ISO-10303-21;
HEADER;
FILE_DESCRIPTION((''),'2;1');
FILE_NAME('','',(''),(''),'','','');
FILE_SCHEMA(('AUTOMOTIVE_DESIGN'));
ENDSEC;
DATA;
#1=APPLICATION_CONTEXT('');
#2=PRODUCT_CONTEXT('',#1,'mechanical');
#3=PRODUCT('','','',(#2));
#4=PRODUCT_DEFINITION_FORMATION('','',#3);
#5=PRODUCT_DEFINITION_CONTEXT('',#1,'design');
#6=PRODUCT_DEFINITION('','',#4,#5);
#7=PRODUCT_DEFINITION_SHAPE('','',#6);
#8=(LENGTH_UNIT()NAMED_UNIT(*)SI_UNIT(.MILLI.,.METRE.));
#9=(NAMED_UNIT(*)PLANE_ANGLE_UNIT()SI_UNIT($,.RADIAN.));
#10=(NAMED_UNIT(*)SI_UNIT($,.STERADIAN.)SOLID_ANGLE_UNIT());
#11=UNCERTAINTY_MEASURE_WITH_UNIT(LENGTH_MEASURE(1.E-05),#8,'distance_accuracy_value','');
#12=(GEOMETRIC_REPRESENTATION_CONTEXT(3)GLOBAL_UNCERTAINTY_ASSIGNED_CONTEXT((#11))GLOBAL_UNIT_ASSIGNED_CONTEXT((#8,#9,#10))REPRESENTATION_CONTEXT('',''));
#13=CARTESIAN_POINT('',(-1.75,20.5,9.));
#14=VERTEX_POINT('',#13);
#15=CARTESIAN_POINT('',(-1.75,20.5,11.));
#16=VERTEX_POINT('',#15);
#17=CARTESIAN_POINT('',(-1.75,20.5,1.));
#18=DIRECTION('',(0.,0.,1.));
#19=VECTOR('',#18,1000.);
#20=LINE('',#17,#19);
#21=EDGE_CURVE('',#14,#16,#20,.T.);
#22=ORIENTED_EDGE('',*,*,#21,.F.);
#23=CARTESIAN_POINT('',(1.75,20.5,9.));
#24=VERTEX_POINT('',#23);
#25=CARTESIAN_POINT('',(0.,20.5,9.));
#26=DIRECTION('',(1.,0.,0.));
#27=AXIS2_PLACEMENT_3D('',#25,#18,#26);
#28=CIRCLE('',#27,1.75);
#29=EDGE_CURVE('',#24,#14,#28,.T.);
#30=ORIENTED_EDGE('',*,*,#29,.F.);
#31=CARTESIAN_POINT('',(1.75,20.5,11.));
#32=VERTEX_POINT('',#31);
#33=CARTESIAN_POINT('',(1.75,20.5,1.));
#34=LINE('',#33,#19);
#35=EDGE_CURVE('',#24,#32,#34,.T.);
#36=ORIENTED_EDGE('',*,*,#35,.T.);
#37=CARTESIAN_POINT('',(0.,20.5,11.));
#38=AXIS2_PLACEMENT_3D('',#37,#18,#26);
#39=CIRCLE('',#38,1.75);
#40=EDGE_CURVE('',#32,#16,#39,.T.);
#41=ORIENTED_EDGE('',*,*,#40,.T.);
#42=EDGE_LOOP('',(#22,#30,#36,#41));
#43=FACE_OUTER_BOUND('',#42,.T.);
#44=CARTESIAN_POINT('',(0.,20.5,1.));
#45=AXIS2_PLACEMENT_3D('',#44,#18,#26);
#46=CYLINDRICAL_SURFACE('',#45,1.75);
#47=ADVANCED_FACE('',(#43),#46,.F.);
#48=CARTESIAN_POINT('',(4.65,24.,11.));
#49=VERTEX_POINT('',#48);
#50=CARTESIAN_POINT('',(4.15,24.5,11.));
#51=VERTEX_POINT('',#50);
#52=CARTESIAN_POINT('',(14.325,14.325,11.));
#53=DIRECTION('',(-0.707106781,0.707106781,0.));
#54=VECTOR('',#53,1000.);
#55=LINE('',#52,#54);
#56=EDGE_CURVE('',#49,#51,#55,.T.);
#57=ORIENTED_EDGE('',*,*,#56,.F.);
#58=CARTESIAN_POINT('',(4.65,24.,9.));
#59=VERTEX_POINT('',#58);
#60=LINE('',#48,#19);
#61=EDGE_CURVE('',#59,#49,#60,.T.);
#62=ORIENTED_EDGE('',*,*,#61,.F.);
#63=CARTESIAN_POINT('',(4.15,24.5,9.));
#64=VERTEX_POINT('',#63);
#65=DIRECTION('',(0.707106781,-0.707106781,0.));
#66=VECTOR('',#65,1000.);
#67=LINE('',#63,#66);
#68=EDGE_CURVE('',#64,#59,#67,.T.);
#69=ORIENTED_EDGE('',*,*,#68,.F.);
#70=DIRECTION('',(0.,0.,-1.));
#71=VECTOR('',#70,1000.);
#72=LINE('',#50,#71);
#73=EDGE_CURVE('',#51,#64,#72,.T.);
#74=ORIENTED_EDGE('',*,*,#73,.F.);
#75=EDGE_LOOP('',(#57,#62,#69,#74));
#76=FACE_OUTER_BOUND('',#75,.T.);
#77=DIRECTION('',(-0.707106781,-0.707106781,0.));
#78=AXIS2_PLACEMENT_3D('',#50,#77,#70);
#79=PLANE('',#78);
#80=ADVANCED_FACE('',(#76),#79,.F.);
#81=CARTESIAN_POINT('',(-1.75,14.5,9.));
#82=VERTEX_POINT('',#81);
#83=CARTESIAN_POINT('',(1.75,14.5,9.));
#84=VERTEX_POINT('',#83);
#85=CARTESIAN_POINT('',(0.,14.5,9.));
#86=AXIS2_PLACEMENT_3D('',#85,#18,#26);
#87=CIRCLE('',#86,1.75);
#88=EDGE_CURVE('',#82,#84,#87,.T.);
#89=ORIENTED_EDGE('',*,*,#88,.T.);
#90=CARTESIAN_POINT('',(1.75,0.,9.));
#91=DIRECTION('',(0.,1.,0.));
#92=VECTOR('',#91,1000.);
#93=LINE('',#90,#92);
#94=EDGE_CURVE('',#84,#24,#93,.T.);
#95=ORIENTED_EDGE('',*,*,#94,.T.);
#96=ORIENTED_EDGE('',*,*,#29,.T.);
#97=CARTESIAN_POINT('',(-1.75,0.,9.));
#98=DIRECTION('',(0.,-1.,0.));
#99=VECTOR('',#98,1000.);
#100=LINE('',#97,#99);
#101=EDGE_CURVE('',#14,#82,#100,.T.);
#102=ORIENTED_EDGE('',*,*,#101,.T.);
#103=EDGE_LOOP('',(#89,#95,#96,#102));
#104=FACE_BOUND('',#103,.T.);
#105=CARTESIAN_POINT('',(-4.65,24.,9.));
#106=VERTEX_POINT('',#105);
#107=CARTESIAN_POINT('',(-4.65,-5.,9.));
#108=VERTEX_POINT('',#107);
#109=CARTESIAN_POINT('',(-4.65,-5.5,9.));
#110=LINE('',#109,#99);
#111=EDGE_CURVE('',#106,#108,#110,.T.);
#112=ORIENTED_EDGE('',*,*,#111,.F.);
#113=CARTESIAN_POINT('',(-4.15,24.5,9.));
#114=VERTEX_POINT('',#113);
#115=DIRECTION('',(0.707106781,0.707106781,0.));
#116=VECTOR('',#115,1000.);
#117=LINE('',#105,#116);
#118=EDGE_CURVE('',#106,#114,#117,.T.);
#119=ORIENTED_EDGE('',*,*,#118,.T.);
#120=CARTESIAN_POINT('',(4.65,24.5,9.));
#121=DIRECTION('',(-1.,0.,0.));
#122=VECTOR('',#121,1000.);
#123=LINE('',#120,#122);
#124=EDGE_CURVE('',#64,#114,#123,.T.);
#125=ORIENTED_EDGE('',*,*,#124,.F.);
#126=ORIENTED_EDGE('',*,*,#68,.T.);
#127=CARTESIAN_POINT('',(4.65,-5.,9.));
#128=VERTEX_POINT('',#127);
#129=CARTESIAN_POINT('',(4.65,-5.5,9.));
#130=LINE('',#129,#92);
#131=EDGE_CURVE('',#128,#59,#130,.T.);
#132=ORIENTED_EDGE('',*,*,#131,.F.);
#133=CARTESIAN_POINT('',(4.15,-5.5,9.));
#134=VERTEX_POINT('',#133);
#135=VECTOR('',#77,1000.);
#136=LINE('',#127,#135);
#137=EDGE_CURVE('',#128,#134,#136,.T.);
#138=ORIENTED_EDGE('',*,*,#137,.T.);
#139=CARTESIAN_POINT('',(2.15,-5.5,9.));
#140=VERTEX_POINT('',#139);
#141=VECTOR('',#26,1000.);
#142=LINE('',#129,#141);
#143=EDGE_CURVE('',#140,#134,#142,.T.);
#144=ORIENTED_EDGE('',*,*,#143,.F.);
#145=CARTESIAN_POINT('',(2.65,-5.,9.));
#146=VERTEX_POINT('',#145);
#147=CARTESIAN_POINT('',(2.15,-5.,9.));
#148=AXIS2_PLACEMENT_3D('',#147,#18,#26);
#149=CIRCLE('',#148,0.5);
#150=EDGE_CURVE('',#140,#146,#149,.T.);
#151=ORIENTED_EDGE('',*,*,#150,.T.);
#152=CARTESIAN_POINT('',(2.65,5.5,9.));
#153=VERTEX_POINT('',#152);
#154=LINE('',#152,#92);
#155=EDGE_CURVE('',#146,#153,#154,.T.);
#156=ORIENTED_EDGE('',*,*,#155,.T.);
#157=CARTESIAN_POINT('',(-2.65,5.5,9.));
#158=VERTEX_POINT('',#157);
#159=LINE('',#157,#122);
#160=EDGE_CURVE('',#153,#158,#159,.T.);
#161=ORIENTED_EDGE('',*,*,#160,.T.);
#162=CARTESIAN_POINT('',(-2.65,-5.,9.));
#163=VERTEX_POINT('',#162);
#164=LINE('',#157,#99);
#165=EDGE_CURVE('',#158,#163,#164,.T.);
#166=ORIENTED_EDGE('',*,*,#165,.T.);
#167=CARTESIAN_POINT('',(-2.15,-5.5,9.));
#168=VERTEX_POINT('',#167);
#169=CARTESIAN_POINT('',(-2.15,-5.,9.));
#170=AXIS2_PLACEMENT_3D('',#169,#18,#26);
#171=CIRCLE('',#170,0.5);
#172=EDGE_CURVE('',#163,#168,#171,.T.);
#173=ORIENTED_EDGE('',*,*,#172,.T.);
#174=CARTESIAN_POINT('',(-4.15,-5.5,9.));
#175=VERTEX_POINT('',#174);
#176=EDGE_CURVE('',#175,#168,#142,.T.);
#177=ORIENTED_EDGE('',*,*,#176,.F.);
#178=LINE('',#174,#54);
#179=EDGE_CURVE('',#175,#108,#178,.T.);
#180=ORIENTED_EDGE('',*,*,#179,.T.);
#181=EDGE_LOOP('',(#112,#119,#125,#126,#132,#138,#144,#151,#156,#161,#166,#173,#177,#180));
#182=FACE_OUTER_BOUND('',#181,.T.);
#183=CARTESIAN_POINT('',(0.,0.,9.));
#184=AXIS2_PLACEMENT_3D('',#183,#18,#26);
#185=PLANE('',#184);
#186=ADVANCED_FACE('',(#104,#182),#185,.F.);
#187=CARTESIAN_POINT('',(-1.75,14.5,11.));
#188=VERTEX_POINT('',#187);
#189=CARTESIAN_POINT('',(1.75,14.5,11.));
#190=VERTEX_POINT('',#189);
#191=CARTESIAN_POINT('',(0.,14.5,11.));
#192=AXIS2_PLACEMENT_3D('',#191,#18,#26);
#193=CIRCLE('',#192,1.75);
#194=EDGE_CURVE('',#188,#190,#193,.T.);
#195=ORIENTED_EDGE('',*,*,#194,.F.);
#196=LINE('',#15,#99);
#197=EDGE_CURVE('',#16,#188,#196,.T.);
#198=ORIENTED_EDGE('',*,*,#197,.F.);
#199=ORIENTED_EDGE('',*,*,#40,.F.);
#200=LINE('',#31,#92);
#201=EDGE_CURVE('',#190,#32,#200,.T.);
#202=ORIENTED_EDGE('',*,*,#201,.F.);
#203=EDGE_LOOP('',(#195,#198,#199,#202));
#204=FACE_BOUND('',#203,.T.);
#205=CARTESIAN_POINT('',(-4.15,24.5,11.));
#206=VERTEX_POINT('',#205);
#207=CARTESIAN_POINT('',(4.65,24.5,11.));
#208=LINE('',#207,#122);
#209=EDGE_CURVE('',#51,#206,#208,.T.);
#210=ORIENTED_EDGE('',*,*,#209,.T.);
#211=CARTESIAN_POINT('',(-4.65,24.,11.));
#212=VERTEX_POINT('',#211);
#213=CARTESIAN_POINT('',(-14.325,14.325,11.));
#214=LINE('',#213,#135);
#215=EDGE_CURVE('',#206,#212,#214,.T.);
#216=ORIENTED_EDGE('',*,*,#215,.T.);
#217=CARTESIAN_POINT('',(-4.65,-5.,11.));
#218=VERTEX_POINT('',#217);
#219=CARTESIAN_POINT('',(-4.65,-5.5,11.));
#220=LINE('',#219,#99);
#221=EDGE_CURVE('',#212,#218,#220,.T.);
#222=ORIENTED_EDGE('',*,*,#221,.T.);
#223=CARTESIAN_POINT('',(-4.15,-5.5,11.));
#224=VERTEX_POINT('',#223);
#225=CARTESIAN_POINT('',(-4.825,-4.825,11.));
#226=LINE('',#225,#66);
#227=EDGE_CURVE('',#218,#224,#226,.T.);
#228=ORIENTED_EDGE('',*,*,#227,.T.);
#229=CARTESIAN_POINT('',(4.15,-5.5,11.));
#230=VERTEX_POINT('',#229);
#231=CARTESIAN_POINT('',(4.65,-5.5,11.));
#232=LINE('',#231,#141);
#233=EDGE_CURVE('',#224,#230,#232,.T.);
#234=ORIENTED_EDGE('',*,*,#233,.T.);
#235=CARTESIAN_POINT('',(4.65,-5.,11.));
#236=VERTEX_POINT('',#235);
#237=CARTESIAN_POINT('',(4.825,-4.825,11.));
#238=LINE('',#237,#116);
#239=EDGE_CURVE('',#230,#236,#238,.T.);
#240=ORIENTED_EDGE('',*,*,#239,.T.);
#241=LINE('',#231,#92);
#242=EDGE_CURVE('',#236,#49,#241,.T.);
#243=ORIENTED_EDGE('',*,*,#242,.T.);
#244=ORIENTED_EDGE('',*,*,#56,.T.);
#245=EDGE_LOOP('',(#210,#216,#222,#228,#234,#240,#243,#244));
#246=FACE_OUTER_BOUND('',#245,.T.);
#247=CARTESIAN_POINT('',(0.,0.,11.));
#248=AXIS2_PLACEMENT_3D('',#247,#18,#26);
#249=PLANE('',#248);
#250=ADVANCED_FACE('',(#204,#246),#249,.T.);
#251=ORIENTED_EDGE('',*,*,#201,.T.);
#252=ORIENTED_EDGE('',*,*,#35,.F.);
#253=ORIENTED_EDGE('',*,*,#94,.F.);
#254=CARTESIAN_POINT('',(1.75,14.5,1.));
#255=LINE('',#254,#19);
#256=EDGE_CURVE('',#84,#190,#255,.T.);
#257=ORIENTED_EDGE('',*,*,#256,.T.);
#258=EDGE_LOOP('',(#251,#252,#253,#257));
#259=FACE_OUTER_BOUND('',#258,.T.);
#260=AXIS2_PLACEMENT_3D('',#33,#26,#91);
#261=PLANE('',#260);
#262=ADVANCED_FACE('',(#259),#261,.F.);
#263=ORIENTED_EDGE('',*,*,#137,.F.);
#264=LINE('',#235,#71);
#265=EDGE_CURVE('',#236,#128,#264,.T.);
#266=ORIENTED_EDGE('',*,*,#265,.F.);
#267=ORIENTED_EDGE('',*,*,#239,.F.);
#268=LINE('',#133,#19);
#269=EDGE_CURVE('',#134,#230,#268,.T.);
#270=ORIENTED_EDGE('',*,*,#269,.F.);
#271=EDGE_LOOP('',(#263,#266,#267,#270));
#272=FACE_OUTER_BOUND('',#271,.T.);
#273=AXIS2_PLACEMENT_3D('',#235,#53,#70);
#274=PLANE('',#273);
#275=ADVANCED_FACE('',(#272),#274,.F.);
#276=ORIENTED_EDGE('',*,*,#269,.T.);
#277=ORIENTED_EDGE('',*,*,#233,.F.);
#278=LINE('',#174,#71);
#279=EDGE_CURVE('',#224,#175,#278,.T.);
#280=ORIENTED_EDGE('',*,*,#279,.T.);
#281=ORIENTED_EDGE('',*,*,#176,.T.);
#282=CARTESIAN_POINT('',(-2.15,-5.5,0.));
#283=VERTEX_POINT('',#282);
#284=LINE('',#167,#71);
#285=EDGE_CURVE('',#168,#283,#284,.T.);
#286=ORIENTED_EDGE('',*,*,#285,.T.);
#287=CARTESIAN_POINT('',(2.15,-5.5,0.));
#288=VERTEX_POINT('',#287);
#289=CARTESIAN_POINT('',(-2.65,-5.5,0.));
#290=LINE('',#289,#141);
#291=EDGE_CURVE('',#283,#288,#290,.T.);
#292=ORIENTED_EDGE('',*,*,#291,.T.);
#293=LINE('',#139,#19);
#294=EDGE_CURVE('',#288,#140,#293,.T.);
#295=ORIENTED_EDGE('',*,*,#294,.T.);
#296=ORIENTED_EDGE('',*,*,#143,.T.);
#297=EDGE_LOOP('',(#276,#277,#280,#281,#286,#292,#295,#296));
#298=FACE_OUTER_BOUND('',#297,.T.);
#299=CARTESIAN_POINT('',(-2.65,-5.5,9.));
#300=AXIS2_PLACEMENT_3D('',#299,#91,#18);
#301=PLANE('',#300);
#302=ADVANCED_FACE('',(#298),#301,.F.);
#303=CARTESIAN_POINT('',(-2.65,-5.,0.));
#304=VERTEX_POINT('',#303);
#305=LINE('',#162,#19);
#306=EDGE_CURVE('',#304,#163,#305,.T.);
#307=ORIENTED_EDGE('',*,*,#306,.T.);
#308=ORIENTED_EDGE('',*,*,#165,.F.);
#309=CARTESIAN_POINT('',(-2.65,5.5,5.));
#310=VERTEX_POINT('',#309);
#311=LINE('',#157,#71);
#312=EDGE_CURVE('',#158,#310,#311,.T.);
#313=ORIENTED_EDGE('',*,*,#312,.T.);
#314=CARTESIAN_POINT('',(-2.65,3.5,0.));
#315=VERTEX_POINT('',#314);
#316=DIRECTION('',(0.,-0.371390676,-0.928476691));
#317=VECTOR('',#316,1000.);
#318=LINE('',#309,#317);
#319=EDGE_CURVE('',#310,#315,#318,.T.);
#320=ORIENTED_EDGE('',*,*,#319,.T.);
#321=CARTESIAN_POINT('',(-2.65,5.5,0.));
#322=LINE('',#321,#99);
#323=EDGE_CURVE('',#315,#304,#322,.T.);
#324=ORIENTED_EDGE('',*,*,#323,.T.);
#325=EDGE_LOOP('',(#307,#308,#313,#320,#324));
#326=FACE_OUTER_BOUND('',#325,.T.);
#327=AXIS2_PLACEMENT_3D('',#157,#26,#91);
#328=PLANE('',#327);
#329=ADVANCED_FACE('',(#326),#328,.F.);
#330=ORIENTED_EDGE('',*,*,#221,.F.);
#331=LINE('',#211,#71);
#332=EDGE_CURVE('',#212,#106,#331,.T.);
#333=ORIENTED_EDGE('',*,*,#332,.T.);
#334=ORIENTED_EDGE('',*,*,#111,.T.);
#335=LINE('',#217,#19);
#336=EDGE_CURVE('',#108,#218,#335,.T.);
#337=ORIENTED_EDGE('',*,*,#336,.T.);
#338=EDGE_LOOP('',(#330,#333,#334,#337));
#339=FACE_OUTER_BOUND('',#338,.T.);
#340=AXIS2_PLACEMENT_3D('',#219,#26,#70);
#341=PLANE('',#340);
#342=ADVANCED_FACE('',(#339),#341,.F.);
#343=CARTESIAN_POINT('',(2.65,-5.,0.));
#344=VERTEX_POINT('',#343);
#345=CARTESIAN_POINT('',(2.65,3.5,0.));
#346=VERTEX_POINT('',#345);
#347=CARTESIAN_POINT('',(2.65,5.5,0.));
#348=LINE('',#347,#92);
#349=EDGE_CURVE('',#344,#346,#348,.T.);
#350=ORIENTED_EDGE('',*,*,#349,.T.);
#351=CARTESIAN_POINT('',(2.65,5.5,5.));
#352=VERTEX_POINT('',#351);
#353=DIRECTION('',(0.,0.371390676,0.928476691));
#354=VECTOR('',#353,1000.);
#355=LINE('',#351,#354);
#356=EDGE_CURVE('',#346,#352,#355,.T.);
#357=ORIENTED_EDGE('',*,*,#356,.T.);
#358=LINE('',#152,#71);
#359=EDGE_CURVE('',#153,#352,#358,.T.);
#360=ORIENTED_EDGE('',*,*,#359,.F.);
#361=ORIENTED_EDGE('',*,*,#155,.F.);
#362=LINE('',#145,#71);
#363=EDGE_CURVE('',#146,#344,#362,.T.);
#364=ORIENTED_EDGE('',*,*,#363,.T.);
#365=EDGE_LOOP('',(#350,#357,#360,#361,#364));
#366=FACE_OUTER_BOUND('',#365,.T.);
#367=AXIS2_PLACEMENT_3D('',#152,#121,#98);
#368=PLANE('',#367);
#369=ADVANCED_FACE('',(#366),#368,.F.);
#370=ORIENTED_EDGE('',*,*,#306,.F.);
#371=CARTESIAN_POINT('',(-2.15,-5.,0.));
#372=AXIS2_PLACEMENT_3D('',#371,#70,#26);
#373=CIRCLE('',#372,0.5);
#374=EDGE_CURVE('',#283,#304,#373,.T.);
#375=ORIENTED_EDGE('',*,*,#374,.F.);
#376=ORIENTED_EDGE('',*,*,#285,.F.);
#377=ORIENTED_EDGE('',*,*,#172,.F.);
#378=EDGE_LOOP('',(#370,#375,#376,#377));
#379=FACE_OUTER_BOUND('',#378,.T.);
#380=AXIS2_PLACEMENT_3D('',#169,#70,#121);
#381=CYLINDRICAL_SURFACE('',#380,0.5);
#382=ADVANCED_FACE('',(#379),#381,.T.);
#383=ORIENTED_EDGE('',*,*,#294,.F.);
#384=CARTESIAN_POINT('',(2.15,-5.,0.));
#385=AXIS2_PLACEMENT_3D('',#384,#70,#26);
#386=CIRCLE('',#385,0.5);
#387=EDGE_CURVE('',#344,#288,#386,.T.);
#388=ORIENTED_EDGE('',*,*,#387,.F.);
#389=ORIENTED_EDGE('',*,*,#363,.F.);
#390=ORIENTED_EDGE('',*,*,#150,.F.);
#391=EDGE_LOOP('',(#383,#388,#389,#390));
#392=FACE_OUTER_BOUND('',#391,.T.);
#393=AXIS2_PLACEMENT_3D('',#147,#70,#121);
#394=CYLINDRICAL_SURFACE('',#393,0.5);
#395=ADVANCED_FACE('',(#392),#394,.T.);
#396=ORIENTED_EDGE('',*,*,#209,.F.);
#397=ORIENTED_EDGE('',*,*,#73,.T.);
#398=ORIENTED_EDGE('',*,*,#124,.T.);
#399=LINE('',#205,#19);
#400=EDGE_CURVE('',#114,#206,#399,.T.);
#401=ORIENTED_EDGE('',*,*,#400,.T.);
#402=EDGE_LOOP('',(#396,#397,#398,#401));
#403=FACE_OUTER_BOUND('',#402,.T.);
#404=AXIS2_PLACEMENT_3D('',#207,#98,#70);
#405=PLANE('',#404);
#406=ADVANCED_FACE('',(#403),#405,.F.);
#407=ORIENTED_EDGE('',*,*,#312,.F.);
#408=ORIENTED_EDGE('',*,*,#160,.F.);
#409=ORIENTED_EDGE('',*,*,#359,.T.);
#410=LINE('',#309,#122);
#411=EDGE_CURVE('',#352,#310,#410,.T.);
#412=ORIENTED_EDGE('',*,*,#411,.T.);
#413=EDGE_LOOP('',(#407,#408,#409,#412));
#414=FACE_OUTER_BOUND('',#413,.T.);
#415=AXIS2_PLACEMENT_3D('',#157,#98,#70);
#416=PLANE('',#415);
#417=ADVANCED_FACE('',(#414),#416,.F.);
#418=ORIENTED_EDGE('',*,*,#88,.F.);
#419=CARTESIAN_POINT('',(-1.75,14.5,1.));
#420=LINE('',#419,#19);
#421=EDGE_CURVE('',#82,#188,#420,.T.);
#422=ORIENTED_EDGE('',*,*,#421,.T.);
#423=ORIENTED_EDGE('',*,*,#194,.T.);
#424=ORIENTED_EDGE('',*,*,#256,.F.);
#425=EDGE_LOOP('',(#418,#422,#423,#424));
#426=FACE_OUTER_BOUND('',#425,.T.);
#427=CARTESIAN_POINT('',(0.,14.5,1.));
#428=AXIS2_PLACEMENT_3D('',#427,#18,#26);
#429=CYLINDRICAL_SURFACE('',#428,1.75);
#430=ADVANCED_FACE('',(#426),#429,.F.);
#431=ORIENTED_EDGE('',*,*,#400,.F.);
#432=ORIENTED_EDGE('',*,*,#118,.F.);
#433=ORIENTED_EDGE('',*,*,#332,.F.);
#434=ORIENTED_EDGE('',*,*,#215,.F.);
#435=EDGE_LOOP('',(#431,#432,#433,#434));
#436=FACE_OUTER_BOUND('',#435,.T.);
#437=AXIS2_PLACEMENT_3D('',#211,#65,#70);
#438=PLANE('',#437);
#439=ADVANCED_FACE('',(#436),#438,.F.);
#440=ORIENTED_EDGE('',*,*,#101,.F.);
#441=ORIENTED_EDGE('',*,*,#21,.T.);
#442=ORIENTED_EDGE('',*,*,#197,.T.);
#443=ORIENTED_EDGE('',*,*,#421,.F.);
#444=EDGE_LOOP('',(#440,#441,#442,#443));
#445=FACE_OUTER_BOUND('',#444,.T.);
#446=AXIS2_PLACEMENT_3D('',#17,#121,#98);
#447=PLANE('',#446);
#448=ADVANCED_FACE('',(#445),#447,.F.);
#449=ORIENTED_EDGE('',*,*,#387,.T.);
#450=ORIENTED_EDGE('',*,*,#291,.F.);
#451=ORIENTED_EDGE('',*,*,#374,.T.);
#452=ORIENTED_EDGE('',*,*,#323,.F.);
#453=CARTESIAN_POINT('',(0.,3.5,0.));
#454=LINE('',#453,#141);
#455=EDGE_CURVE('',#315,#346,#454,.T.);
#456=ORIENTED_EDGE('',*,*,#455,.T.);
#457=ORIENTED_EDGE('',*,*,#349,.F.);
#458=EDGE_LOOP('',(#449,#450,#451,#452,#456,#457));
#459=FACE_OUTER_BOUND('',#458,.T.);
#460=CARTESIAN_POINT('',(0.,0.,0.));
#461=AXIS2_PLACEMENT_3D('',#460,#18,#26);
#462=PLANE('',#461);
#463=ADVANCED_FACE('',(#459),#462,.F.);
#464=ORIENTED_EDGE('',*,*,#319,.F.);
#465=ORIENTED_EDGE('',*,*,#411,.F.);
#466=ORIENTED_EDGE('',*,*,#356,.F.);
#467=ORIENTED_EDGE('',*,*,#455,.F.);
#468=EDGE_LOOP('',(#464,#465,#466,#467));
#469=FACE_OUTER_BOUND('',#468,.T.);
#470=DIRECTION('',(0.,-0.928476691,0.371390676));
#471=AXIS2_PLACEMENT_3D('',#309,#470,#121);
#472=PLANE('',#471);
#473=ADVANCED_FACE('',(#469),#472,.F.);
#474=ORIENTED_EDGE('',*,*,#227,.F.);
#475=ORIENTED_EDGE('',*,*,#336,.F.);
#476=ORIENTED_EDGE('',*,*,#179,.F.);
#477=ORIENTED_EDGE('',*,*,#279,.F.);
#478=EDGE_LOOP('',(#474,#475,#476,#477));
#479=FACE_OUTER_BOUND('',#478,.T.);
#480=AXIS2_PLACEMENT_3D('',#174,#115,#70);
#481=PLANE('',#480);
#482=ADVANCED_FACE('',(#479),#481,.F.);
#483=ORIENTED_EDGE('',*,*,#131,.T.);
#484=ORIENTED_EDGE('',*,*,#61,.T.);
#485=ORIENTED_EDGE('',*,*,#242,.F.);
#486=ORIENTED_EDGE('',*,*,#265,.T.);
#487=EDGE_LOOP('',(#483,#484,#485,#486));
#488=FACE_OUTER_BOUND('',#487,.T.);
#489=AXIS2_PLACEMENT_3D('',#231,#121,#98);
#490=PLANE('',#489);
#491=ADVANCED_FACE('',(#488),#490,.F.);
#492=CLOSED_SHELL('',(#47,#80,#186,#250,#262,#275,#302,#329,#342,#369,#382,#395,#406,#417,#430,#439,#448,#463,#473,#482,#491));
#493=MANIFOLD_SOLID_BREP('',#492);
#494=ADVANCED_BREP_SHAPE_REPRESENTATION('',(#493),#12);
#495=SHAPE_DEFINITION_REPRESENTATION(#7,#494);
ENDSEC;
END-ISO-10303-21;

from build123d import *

# Parameters (mm, degrees)
SKETCH1_W           = 5.3
SKETCH1_H           = 11
BOSS_EXTRUDE1_DEPTH = 9
SKETCH2_W           = 9.3
SKETCH2_H           = 30
BOSS_EXTRUDE2_DEPTH = 2
CUT_EXTRUDE1_DEPTH  = 10
CHAMFER1_SIZE       = 0.5
FILLET1_R           = 0.5
CHAMFER2_SIZE       = 2
CHAMFER2_SIZE2      = 5


with BuildPart() as part:
    # Sketch1 → Boss-Extrude1 (new body)
    with BuildSketch(Plane.XY):
        Rectangle(SKETCH1_W, SKETCH1_H)
    extrude(amount=BOSS_EXTRUDE1_DEPTH)

    # Sketch2 → Boss-Extrude2 (add)
    with BuildSketch(Plane.XY.offset(9)):
        with Locations((0, 9.5)):
            Rectangle(SKETCH2_W, SKETCH2_H)
    extrude(amount=BOSS_EXTRUDE2_DEPTH)

    # Sketch3 → Cut-Extrude1 (cut)
    with BuildSketch(Plane.XY.offset(11)):
        with BuildLine():
            Line((1.75, 20.5), (1.75, 14.5))
            ThreePointArc((1.75, 14.5), (0, 12.75), (-1.75, 14.5))
            Line((-1.75, 14.5), (-1.75, 20.5))
            ThreePointArc((-1.75, 20.5), (0, 22.25), (1.75, 20.5))
        make_face()
    extrude(amount=-CUT_EXTRUDE1_DEPTH, mode=Mode.SUBTRACT)

    # Chamfer1
    chamfer1_edges = [part.edges().sort_by_distance(p)[0] for p in [
        (-4.65, -5.5, 10),
        (4.65, -5.5, 10),
        (4.65, 24.5, 10),
        (-4.65, 24.5, 10),
    ]]
    chamfer(chamfer1_edges, length=CHAMFER1_SIZE)

    # Fillet1
    fillet1_edges = [part.edges().sort_by_distance(p)[0] for p in [
        (2.65, -5.5, 4.5),
        (-2.65, -5.5, 4.5),
    ]]
    fillet(fillet1_edges, radius=FILLET1_R)

    # Chamfer2
    chamfer2_edges = [part.edges().sort_by_distance(p)[0] for p in [
        (0, 5.5, 0),
    ]]
    chamfer2_side = [part.faces().sort_by_distance(p)[0] for p in [
        (0, 0.00993546, 0),
    ]]
    chamfer(chamfer2_edges, length=CHAMFER2_SIZE, length2=CHAMFER2_SIZE2, reference=chamfer2_side[0])


solid = part.part
